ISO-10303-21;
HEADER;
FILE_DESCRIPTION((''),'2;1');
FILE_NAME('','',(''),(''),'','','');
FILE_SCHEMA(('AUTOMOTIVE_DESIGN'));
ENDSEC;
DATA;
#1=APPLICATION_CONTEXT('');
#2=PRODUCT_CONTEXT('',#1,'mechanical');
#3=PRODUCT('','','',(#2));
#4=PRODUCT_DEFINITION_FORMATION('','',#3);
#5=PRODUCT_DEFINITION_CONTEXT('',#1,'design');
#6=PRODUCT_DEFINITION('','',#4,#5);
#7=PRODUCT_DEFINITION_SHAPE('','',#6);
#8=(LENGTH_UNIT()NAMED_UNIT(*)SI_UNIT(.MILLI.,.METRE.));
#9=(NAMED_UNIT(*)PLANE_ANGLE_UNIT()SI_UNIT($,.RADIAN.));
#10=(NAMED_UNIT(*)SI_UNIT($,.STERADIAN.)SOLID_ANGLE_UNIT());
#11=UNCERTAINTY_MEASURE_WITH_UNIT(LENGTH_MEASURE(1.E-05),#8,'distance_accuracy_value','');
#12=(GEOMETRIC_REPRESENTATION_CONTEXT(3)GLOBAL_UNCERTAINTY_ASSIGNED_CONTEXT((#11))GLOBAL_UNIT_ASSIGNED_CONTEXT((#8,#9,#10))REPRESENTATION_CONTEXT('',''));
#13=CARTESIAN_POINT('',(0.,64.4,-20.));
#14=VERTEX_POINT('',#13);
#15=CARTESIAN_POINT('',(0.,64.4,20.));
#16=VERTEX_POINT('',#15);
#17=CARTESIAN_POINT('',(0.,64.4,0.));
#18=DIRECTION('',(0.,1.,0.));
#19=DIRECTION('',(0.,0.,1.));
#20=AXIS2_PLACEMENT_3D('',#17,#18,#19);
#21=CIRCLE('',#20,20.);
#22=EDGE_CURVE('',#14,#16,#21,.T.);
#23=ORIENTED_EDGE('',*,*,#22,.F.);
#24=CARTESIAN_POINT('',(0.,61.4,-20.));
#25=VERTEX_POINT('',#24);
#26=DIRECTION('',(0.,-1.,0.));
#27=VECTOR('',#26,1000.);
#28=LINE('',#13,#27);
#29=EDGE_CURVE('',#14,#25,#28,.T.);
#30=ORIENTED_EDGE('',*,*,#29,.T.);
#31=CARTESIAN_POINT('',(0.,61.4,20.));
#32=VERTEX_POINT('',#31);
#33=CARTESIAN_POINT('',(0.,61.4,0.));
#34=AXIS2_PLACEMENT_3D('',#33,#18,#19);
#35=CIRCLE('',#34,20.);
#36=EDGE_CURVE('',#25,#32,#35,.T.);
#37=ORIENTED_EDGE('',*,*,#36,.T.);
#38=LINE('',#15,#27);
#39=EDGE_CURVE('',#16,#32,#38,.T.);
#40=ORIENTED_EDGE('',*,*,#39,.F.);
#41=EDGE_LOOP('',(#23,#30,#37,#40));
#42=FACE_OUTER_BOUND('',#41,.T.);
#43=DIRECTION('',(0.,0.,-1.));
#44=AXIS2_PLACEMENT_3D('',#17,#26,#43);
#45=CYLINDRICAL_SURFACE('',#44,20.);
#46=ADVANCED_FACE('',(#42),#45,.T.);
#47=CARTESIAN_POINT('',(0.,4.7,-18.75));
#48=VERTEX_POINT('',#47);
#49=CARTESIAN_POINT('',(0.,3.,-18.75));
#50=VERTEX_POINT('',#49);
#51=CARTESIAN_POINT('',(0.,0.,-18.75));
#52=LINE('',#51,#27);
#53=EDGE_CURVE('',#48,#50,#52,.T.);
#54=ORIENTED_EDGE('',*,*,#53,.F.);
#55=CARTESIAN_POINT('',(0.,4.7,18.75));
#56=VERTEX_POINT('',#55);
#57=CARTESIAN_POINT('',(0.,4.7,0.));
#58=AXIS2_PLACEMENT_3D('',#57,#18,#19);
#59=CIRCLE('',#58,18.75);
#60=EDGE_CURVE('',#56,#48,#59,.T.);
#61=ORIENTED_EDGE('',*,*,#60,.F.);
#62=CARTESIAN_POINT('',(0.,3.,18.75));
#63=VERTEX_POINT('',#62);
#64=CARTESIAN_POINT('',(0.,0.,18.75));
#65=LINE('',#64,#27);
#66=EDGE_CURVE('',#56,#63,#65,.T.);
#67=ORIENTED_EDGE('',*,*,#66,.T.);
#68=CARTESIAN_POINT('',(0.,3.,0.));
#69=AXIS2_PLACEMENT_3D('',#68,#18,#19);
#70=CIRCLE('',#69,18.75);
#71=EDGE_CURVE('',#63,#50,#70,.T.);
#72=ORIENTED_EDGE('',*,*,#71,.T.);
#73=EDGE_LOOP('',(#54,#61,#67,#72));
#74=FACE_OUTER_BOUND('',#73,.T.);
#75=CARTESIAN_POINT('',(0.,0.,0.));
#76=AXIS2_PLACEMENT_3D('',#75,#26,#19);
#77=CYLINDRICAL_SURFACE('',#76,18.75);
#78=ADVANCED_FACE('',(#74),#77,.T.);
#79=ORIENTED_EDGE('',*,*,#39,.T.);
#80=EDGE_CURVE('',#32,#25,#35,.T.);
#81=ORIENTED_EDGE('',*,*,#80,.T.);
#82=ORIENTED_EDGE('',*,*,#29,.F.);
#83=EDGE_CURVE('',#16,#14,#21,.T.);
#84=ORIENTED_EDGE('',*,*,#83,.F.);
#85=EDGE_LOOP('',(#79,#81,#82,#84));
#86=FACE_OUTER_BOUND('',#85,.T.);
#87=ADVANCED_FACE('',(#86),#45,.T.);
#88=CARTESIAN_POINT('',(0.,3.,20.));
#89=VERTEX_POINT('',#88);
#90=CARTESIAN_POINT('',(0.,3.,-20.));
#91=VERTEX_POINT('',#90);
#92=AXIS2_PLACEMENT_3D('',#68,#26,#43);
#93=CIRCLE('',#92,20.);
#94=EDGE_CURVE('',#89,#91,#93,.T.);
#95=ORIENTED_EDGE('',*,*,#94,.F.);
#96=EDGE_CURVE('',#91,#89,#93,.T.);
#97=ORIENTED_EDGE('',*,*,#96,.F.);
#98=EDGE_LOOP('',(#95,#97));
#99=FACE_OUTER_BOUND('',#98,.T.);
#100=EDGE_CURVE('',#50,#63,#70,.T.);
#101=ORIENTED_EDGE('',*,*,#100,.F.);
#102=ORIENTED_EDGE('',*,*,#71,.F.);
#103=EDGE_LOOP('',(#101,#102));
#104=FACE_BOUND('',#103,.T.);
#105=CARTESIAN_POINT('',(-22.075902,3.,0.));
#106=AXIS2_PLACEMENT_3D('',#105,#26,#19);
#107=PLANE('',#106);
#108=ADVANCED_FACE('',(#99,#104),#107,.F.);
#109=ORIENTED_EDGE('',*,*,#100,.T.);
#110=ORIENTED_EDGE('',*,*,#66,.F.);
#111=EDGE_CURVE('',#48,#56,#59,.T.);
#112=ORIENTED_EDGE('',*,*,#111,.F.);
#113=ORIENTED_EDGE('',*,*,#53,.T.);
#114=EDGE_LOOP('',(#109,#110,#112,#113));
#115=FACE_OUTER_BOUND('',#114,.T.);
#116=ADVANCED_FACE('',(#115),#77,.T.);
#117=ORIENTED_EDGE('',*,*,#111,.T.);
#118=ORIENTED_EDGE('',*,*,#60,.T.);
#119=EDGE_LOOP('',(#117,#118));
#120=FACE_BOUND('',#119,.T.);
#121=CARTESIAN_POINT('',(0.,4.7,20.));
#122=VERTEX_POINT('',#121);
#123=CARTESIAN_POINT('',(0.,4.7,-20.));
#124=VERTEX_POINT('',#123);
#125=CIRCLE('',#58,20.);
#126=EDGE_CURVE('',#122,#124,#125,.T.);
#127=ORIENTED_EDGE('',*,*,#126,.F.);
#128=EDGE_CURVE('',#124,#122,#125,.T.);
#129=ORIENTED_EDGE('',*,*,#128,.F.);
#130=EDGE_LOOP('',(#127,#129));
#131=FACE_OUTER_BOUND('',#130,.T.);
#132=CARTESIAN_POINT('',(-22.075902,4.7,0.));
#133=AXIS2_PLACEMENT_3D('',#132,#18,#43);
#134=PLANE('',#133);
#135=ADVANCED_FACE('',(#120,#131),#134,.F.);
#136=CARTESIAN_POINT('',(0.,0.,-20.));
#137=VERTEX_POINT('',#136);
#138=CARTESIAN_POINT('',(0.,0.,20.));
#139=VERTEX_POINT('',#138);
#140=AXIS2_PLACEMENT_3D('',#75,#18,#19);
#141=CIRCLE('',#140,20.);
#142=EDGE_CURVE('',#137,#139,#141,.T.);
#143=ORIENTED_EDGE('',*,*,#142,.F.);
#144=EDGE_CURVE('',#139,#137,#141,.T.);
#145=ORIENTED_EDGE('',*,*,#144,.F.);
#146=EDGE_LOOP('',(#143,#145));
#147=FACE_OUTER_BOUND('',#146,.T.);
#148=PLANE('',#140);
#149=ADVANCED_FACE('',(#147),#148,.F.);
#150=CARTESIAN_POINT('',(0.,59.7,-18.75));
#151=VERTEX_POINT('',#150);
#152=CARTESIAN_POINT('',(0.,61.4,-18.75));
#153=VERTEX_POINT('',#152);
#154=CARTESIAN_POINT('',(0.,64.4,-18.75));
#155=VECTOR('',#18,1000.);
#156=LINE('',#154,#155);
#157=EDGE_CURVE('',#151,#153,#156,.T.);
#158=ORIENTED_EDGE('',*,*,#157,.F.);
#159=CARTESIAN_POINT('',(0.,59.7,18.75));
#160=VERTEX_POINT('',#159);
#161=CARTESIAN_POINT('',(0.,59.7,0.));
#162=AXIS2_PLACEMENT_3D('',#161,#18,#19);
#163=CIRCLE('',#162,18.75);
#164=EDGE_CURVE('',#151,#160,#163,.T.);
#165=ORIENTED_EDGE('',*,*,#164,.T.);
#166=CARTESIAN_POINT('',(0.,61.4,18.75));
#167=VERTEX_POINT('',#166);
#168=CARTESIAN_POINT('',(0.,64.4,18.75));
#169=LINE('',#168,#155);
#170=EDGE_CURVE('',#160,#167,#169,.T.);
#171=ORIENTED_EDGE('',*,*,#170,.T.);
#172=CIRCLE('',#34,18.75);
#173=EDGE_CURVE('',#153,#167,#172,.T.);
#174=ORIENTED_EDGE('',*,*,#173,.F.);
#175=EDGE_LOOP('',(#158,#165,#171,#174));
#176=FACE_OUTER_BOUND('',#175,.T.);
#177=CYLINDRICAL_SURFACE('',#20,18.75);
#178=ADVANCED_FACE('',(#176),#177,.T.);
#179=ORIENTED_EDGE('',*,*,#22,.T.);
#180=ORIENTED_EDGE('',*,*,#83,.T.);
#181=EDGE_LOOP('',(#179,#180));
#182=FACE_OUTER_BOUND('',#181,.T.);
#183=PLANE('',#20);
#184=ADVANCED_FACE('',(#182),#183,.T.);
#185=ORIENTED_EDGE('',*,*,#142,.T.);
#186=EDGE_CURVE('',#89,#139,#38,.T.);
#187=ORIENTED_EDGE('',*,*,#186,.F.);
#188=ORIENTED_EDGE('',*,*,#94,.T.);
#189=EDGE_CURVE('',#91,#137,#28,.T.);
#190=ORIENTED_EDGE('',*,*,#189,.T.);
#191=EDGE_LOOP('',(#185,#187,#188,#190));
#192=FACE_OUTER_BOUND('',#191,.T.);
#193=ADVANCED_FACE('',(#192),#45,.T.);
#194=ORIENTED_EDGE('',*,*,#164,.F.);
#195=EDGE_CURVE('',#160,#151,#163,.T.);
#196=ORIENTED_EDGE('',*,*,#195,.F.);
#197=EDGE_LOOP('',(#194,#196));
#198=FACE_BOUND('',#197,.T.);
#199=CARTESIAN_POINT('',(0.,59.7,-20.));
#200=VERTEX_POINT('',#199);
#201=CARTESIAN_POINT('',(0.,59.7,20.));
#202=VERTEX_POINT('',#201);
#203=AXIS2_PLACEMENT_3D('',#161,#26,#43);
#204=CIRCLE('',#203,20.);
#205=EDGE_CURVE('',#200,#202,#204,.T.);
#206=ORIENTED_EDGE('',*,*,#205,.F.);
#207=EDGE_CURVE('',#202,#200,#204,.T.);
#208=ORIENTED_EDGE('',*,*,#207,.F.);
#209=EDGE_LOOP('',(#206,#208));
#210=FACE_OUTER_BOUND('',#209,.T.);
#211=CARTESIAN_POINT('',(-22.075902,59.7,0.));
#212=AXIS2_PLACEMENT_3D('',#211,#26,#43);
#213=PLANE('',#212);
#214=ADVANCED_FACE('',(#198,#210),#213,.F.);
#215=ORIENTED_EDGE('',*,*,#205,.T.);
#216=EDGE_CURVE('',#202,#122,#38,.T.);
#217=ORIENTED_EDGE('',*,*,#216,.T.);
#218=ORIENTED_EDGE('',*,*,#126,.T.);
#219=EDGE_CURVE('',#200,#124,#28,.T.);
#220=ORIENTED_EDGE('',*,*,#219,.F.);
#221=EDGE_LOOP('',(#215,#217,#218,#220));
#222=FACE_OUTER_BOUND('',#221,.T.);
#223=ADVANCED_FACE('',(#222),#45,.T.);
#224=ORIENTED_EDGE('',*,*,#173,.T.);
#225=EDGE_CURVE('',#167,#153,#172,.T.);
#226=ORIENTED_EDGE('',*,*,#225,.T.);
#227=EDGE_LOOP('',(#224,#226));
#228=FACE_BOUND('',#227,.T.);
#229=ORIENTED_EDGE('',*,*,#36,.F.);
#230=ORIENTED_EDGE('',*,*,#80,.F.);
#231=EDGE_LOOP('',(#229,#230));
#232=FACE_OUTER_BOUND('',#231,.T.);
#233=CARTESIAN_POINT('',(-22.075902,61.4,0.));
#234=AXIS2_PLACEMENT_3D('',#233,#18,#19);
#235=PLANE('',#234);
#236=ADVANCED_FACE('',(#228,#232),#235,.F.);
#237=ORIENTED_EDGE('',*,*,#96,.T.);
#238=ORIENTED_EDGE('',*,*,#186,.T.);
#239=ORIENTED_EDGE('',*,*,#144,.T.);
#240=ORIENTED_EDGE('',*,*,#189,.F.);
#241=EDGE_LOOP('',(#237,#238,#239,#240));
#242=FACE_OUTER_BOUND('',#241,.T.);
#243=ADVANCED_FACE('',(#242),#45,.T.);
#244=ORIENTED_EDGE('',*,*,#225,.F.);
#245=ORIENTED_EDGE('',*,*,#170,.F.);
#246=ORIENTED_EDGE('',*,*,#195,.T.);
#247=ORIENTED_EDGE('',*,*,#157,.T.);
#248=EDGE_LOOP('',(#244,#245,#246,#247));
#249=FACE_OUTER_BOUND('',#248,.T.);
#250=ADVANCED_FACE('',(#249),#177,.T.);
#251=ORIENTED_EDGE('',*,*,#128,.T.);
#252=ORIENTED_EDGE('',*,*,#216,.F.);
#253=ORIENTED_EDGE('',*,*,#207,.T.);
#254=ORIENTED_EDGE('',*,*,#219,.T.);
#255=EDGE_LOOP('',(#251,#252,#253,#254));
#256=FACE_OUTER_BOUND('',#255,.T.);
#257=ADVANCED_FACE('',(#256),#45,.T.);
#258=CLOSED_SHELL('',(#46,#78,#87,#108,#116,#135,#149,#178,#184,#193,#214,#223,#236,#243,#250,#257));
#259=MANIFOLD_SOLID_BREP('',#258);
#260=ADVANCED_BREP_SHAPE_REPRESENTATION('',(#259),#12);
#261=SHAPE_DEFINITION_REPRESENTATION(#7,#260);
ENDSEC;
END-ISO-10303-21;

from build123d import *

# Parameters (mm, degrees)
SKETCH_1_R      = 20
EXTRUDE_1_DEPTH = 64.4
SKETCH_2_W      = 3.325902221
SKETCH_2_H      = 1.7


with BuildPart() as part:
    # 草图1 → 凸台-拉伸1 (new body)
    with BuildSketch(Plane(origin=(0, 0, 0), x_dir=(1, 0, 0), z_dir=(0, 1, 0))):
        with Locations(Location((0, 0, 0), (0, 0, 270))):
            Circle(SKETCH_1_R)
    extrude(amount=EXTRUDE_1_DEPTH)

    # 草图2 → 切除-旋转1 (revolve, cut)
    with BuildSketch(Plane.XY, mode=Mode.PRIVATE) as cut_revolve_1_sk:
        with Locations((-20.41295111, 60.55)):
            Rectangle(SKETCH_2_W, SKETCH_2_H)
    cut_revolve_1 = revolve(cut_revolve_1_sk.sketch.rotate(Axis((0, 64.4, 0), (0, -1, 0)), 270), axis=Axis((0, 64.4, 0), (0, -1, 0)), mode=Mode.SUBTRACT)

    # 镜向1: 切除-旋转1 across plane
    add(cut_revolve_1.mirror(Plane(origin=(0, 32.2, 0), x_dir=(0, 0, 1), z_dir=(0, -1, 0))), mode=Mode.SUBTRACT)


solid = part.part
